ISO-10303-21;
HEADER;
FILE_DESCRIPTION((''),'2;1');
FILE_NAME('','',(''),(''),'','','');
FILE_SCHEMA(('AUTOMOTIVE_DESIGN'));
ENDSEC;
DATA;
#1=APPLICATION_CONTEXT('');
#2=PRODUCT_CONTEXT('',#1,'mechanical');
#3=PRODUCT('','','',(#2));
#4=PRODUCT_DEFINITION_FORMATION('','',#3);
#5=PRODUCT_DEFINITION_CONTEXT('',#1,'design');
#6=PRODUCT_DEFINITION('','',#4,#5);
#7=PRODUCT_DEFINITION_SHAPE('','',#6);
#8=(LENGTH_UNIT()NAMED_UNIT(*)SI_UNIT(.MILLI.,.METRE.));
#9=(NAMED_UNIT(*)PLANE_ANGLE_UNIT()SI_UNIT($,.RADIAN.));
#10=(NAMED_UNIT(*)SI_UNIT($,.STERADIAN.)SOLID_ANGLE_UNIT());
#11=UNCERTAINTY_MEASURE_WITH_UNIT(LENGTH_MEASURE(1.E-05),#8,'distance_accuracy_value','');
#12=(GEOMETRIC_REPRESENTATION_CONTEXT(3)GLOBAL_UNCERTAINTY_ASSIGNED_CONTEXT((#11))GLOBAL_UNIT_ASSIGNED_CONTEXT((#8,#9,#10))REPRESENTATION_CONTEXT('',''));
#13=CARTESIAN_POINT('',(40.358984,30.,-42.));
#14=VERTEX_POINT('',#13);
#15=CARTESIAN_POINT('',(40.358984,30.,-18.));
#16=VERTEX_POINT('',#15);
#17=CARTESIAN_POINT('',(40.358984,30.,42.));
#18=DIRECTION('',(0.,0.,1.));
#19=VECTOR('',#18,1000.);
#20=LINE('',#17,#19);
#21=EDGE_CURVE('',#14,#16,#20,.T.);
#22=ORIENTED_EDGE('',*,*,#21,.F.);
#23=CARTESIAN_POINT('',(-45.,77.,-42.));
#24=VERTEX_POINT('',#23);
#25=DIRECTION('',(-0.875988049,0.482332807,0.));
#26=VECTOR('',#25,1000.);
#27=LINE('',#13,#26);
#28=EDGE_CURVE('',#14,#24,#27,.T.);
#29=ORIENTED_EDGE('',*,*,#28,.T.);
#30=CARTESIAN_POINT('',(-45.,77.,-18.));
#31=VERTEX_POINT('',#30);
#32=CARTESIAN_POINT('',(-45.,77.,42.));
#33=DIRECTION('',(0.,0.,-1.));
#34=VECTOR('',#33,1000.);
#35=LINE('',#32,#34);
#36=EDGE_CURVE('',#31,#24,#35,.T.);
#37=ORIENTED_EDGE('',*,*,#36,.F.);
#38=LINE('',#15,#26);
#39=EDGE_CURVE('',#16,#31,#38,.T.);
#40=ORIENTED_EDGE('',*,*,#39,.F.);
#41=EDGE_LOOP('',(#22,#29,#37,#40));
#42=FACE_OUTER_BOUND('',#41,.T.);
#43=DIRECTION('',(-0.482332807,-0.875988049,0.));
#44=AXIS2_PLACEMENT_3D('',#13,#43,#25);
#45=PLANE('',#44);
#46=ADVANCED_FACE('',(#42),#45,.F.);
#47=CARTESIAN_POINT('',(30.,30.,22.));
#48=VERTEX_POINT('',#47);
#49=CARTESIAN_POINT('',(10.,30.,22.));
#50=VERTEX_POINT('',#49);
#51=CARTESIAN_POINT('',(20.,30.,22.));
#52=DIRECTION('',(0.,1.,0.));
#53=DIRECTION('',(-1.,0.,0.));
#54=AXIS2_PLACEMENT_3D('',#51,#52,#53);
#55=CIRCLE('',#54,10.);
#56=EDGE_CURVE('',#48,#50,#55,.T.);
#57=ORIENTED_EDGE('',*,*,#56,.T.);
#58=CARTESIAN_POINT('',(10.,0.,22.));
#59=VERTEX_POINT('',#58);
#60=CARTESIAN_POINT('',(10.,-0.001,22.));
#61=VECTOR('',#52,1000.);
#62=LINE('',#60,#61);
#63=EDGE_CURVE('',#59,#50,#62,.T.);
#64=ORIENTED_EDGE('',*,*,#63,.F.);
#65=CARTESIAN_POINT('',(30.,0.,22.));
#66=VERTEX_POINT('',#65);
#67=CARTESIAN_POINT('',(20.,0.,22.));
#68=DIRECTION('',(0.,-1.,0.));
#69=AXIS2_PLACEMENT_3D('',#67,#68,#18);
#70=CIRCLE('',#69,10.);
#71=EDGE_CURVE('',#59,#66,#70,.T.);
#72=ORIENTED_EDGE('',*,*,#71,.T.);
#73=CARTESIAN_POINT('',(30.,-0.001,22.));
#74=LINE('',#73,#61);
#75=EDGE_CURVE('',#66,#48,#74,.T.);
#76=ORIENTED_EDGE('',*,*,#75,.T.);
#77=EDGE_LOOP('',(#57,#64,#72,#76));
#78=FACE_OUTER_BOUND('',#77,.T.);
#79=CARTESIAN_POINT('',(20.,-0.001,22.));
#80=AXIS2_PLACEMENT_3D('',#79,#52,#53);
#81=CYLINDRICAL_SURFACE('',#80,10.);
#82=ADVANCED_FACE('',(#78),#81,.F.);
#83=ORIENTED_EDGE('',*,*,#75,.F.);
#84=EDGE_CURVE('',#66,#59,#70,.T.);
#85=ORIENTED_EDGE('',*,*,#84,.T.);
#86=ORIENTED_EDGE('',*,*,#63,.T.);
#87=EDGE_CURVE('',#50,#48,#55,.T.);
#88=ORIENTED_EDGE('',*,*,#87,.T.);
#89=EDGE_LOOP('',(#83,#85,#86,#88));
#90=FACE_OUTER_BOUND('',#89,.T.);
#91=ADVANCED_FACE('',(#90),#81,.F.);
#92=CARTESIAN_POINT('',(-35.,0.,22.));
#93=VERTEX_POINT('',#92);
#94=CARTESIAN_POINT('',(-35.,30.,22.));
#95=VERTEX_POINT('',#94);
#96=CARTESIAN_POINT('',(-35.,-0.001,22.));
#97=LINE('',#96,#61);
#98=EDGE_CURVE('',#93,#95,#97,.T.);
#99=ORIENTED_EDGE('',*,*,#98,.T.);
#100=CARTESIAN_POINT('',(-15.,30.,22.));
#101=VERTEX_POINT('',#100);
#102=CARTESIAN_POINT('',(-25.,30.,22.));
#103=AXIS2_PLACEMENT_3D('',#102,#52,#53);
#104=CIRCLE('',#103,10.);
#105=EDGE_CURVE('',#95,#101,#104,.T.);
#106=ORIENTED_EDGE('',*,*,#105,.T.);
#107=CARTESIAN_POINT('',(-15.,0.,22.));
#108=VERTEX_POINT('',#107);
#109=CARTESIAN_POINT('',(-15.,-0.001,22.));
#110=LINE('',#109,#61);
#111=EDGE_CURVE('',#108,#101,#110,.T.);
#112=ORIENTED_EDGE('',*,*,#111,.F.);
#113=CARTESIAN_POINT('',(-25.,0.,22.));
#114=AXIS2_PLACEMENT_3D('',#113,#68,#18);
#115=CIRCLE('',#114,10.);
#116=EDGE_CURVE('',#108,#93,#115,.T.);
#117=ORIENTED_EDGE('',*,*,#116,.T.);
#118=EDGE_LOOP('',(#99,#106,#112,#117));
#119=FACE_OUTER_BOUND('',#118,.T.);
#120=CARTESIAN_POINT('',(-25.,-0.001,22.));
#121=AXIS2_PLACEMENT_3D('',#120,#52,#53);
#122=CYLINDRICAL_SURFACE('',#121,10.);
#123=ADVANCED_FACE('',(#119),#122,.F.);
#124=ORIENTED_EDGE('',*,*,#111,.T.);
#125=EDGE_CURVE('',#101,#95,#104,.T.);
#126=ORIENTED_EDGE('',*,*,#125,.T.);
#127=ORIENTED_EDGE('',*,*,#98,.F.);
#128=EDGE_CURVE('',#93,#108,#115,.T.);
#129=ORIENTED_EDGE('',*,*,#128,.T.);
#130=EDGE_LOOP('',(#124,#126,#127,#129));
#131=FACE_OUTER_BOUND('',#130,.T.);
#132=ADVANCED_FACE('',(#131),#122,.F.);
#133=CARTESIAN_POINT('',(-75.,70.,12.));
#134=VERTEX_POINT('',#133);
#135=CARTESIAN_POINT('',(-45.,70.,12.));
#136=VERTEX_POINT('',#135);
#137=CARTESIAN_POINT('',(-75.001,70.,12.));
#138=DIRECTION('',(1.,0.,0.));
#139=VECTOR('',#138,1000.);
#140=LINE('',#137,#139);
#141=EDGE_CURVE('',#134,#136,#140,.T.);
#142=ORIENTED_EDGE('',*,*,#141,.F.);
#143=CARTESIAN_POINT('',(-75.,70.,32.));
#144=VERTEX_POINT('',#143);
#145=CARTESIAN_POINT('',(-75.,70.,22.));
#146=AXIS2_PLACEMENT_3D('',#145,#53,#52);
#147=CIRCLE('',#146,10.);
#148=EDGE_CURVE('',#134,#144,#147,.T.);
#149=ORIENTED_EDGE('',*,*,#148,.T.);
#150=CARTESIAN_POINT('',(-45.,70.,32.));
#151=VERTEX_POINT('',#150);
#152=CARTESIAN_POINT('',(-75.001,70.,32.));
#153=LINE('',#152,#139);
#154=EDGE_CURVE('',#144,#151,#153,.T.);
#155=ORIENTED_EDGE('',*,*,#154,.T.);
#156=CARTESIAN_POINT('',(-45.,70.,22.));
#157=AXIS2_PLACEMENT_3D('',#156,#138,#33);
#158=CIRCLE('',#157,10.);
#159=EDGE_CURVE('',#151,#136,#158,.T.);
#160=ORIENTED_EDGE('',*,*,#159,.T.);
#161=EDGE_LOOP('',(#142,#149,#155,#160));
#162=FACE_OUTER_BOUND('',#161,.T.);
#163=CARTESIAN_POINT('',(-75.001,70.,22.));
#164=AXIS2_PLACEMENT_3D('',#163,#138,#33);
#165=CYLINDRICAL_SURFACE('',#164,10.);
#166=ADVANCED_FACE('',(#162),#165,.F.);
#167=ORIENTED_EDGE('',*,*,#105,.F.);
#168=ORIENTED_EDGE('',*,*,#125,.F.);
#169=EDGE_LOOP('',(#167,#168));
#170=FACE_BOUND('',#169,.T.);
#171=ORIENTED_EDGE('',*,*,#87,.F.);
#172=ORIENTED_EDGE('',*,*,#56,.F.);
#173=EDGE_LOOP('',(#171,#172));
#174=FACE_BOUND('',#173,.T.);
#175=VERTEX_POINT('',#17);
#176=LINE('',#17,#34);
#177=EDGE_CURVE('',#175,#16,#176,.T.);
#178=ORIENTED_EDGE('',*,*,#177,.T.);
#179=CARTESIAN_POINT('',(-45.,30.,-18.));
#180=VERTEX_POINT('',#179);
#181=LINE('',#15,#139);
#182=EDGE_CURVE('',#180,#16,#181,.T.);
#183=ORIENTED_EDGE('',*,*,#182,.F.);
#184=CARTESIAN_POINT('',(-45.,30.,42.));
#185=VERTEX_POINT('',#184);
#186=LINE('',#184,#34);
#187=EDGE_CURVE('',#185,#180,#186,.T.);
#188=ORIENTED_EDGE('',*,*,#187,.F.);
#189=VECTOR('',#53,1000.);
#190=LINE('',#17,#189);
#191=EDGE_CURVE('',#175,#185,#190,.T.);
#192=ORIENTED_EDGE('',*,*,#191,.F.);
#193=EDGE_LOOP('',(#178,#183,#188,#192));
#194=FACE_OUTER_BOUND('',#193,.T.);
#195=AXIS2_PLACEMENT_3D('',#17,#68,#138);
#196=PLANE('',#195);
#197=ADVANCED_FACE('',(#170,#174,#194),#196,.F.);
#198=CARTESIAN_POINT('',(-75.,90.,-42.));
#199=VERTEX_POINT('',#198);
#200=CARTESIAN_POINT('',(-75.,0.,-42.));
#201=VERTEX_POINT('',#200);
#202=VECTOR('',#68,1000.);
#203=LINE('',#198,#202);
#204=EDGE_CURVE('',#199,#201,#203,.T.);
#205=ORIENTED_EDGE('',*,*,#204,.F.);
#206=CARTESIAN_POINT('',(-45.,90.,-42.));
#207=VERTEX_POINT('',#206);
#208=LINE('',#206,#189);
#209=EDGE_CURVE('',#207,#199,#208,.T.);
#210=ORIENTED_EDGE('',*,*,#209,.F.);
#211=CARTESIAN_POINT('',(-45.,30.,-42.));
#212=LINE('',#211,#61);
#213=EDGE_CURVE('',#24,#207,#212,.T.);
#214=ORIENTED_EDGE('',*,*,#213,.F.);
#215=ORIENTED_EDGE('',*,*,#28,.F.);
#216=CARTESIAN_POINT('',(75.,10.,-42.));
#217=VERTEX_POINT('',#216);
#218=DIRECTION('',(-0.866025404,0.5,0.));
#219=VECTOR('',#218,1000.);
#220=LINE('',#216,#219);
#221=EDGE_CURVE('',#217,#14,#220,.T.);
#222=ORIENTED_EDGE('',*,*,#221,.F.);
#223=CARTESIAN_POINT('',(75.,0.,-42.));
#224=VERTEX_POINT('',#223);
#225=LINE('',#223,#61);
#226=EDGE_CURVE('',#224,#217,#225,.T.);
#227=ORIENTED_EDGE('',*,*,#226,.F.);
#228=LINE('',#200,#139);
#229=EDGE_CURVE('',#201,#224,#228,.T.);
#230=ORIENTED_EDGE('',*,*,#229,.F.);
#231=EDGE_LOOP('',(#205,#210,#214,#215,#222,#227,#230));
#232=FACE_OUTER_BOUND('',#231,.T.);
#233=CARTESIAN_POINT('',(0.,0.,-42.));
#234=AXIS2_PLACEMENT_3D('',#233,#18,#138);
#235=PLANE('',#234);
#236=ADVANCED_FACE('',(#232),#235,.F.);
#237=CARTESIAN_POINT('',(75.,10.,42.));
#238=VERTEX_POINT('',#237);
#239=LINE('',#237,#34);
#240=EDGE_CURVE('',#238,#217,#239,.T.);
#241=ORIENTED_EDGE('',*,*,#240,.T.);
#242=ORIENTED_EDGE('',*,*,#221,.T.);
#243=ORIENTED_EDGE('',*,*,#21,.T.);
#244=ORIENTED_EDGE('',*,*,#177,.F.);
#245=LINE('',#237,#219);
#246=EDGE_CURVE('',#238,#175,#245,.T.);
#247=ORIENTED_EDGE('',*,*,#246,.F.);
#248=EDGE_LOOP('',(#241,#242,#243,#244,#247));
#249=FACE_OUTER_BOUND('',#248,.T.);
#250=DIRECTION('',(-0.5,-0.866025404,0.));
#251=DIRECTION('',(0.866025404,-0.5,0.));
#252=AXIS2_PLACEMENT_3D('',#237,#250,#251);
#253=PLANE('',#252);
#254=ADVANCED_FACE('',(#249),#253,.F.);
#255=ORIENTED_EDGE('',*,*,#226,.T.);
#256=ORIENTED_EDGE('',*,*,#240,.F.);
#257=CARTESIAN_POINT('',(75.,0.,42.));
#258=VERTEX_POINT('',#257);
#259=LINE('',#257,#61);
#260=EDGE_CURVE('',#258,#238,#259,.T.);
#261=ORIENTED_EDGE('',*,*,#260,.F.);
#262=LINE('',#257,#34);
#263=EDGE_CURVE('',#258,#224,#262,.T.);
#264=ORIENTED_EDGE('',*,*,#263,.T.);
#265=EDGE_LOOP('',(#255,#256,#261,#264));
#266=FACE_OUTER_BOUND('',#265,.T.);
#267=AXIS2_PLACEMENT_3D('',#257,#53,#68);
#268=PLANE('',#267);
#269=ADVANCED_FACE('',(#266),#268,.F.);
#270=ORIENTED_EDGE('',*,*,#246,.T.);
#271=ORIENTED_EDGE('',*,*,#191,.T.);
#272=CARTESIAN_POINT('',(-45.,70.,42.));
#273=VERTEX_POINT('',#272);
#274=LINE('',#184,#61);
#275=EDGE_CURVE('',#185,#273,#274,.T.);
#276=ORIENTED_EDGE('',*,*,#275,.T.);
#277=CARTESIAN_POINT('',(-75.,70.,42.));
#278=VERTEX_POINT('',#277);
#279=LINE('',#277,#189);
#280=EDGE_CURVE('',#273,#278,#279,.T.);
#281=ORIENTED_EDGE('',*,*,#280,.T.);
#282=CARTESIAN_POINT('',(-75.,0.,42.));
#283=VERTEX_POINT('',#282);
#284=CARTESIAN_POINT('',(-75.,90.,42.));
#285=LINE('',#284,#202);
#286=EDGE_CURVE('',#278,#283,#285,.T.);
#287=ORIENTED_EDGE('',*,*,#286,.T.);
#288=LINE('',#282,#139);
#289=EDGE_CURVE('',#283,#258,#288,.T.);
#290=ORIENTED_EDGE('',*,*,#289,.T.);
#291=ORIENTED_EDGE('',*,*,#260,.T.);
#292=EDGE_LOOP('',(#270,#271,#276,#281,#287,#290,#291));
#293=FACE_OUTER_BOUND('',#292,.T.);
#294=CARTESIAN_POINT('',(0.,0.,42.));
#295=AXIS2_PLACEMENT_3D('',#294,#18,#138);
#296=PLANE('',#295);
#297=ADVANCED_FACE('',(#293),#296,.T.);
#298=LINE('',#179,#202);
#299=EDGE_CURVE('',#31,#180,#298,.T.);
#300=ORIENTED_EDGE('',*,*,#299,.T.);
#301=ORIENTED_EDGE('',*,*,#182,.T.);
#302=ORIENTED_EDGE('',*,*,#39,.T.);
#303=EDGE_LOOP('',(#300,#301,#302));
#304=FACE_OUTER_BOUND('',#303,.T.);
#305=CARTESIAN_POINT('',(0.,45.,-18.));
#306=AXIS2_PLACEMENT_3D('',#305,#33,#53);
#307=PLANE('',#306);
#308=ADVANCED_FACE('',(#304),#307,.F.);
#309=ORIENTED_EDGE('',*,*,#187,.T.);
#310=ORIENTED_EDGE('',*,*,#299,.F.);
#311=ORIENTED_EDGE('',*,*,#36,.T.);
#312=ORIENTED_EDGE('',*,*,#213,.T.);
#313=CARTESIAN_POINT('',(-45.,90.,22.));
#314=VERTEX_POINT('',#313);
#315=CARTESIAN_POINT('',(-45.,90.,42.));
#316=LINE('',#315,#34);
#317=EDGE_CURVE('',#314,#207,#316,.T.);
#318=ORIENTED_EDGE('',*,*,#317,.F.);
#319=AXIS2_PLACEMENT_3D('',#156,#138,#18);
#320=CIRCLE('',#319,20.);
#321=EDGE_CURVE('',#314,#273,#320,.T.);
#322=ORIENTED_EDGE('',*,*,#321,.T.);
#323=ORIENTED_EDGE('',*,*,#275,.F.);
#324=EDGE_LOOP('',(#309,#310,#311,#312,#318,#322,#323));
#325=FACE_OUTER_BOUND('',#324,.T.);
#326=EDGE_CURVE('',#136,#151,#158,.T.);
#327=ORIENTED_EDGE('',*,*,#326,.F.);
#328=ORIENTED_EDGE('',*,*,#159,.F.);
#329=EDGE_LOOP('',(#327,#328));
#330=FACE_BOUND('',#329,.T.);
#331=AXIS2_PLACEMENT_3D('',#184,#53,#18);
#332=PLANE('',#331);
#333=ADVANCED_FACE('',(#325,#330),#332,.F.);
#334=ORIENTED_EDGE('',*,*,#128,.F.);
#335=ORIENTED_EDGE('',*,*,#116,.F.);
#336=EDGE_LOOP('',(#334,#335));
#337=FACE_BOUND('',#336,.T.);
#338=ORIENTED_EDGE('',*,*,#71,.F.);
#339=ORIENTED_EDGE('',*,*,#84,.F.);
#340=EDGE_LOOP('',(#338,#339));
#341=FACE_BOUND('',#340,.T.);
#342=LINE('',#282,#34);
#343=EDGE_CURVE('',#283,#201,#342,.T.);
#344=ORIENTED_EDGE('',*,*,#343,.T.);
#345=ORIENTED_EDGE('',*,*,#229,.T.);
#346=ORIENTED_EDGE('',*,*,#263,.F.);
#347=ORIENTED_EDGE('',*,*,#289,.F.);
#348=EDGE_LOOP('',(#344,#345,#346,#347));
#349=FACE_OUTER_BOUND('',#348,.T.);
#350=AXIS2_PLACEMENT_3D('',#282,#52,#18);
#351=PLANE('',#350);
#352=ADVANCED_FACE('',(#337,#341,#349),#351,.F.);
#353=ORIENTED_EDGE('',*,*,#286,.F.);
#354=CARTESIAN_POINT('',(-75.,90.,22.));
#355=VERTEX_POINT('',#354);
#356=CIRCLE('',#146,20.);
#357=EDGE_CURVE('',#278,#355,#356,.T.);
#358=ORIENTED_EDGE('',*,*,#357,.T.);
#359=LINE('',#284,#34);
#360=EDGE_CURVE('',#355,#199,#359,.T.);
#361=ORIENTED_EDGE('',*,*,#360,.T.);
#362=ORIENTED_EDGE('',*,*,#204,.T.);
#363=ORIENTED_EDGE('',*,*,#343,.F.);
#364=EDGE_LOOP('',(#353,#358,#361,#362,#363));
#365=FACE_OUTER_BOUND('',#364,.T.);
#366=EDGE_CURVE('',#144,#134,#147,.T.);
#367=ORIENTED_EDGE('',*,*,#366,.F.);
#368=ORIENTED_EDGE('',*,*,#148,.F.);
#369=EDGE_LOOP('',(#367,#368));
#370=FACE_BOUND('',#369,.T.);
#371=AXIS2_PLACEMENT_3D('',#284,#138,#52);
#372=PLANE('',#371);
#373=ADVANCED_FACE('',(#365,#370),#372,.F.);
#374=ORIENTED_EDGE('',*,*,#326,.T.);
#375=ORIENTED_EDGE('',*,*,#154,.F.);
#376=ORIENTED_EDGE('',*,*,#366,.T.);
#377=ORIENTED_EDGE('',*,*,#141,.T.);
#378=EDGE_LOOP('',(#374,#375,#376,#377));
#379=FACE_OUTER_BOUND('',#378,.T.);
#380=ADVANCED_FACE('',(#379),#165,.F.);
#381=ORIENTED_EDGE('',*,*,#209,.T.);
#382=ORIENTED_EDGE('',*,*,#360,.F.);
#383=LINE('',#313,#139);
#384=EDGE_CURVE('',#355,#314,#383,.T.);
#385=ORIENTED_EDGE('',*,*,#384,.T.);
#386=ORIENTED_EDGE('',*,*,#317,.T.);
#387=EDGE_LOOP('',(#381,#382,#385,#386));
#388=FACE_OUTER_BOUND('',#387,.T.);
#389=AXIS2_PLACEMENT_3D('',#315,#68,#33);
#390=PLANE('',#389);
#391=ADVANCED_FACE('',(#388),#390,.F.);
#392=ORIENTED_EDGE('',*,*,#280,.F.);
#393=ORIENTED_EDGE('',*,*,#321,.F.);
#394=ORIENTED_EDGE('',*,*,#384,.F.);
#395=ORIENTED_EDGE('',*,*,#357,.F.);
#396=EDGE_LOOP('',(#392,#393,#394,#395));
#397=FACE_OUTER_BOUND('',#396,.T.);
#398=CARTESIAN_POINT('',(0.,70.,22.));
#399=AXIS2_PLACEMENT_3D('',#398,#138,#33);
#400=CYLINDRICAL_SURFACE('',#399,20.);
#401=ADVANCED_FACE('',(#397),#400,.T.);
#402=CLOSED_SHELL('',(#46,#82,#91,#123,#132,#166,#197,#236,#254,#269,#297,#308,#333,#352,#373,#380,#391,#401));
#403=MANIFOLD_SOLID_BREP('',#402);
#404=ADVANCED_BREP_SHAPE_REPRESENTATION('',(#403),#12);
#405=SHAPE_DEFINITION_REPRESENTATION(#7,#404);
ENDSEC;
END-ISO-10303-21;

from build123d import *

# Parameters (mm, degrees)
BRACKET_BODY_DEPTH           = 42
UPRIGHT_TOP_ROUND_R20_R      = 20
SUPPORT_RIB_REACH            = 146.156
SUPPORT_RIB_SKETCH_WALL_W    = 387.75542236
SUPPORT_RIB_SKETCH_WALL_H    = 24
BASE_MOUNTING_HOLES_REACH    = 106.828
BASE_MOUNTING_HOLES_SKETCH_R = 10
UPRIGHT_HOLE_20_REACH        = 157.769
UPRIGHT_HOLE_SKETCH_R        = 10


with BuildPart() as part:
    # Bracket Profile Sketch → Bracket Body (new, symmetric)
    with BuildSketch(Plane.XY):
        Polygon((-75, 90), (-75, 0), (75, 0), (75, 10), (40.358983849, 30), (-45, 30), (-45, 90), align=None)
    extrude(amount=BRACKET_BODY_DEPTH, both=True)

    # Upright Top Round R20
    upright_top_round_r20_edges = [part.edges().sort_by_distance(p)[0] for p in [
        (-60, 90, 42),
    ]]
    fillet(upright_top_round_r20_edges, radius=UPRIGHT_TOP_ROUND_R20_R)

    # Support Rib Sketch wall → Support Rib (add, up to next)
    with BuildSketch(Plane(origin=(-2.320508076, 53.5, -42), x_dir=(-0.875988049468, 0.482332807497, 0), z_dir=(0.482332807497, 0.875988049468, 0)), mode=Mode.PRIVATE) as support_rib_sk1:
        with Locations((0, 12)):
            Rectangle(SUPPORT_RIB_SKETCH_WALL_W, SUPPORT_RIB_SKETCH_WALL_H)
    support_rib_tool1 = extrude(support_rib_sk1.sketch, amount=-SUPPORT_RIB_REACH, mode=Mode.PRIVATE) - part.part
    add(support_rib_tool1.solids().sort_by_distance((-2.320508076, 53.5, -42))[0])

    # Base Mounting Holes Sketch → Base Mounting Holes (cut, up to next)
    with BuildSketch(Plane(origin=(0, 30, 0), x_dir=(1, 0, 0), z_dir=(0, 1, 0)), mode=Mode.PRIVATE) as base_mounting_holes_sk1:
        with Locations(Location((-25, -22, 0), (0, 0, 180))):
            Circle(BASE_MOUNTING_HOLES_SKETCH_R)
    base_mounting_holes_tool1 = extrude(base_mounting_holes_sk1.sketch, amount=-BASE_MOUNTING_HOLES_REACH, mode=Mode.PRIVATE) & part.part
    # Base Mounting Holes Sketch → Base Mounting Holes (cut, up to next)
    with BuildSketch(Plane(origin=(0, 30, 0), x_dir=(1, 0, 0), z_dir=(0, 1, 0)), mode=Mode.PRIVATE) as base_mounting_holes_sk2:
        with Locations(Location((20, -22, 0), (0, 0, 180))):
            Circle(BASE_MOUNTING_HOLES_SKETCH_R)
    base_mounting_holes_tool2 = extrude(base_mounting_holes_sk2.sketch, amount=-BASE_MOUNTING_HOLES_REACH, mode=Mode.PRIVATE) & part.part
    add(base_mounting_holes_tool1.solids().sort_by_distance((-25, 30, 22))[0], mode=Mode.SUBTRACT)
    add(base_mounting_holes_tool2.solids().sort_by_distance((20, 30, 22))[0], mode=Mode.SUBTRACT)

    # Upright Hole Sketch → Upright Hole Ø20 (cut, up to next)
    with BuildSketch(Plane(origin=(-45, 0, 0), x_dir=(0, 0, -1), z_dir=(1, 0, 0)), mode=Mode.PRIVATE) as upright_hole_20_sk1:
        with Locations((-22, 70)):
            Circle(UPRIGHT_HOLE_SKETCH_R)
    upright_hole_20_tool1 = extrude(upright_hole_20_sk1.sketch, amount=-UPRIGHT_HOLE_20_REACH, mode=Mode.PRIVATE) & part.part
    add(upright_hole_20_tool1.solids().sort_by_distance((-45, 70, 22))[0], mode=Mode.SUBTRACT)


solid = part.part
